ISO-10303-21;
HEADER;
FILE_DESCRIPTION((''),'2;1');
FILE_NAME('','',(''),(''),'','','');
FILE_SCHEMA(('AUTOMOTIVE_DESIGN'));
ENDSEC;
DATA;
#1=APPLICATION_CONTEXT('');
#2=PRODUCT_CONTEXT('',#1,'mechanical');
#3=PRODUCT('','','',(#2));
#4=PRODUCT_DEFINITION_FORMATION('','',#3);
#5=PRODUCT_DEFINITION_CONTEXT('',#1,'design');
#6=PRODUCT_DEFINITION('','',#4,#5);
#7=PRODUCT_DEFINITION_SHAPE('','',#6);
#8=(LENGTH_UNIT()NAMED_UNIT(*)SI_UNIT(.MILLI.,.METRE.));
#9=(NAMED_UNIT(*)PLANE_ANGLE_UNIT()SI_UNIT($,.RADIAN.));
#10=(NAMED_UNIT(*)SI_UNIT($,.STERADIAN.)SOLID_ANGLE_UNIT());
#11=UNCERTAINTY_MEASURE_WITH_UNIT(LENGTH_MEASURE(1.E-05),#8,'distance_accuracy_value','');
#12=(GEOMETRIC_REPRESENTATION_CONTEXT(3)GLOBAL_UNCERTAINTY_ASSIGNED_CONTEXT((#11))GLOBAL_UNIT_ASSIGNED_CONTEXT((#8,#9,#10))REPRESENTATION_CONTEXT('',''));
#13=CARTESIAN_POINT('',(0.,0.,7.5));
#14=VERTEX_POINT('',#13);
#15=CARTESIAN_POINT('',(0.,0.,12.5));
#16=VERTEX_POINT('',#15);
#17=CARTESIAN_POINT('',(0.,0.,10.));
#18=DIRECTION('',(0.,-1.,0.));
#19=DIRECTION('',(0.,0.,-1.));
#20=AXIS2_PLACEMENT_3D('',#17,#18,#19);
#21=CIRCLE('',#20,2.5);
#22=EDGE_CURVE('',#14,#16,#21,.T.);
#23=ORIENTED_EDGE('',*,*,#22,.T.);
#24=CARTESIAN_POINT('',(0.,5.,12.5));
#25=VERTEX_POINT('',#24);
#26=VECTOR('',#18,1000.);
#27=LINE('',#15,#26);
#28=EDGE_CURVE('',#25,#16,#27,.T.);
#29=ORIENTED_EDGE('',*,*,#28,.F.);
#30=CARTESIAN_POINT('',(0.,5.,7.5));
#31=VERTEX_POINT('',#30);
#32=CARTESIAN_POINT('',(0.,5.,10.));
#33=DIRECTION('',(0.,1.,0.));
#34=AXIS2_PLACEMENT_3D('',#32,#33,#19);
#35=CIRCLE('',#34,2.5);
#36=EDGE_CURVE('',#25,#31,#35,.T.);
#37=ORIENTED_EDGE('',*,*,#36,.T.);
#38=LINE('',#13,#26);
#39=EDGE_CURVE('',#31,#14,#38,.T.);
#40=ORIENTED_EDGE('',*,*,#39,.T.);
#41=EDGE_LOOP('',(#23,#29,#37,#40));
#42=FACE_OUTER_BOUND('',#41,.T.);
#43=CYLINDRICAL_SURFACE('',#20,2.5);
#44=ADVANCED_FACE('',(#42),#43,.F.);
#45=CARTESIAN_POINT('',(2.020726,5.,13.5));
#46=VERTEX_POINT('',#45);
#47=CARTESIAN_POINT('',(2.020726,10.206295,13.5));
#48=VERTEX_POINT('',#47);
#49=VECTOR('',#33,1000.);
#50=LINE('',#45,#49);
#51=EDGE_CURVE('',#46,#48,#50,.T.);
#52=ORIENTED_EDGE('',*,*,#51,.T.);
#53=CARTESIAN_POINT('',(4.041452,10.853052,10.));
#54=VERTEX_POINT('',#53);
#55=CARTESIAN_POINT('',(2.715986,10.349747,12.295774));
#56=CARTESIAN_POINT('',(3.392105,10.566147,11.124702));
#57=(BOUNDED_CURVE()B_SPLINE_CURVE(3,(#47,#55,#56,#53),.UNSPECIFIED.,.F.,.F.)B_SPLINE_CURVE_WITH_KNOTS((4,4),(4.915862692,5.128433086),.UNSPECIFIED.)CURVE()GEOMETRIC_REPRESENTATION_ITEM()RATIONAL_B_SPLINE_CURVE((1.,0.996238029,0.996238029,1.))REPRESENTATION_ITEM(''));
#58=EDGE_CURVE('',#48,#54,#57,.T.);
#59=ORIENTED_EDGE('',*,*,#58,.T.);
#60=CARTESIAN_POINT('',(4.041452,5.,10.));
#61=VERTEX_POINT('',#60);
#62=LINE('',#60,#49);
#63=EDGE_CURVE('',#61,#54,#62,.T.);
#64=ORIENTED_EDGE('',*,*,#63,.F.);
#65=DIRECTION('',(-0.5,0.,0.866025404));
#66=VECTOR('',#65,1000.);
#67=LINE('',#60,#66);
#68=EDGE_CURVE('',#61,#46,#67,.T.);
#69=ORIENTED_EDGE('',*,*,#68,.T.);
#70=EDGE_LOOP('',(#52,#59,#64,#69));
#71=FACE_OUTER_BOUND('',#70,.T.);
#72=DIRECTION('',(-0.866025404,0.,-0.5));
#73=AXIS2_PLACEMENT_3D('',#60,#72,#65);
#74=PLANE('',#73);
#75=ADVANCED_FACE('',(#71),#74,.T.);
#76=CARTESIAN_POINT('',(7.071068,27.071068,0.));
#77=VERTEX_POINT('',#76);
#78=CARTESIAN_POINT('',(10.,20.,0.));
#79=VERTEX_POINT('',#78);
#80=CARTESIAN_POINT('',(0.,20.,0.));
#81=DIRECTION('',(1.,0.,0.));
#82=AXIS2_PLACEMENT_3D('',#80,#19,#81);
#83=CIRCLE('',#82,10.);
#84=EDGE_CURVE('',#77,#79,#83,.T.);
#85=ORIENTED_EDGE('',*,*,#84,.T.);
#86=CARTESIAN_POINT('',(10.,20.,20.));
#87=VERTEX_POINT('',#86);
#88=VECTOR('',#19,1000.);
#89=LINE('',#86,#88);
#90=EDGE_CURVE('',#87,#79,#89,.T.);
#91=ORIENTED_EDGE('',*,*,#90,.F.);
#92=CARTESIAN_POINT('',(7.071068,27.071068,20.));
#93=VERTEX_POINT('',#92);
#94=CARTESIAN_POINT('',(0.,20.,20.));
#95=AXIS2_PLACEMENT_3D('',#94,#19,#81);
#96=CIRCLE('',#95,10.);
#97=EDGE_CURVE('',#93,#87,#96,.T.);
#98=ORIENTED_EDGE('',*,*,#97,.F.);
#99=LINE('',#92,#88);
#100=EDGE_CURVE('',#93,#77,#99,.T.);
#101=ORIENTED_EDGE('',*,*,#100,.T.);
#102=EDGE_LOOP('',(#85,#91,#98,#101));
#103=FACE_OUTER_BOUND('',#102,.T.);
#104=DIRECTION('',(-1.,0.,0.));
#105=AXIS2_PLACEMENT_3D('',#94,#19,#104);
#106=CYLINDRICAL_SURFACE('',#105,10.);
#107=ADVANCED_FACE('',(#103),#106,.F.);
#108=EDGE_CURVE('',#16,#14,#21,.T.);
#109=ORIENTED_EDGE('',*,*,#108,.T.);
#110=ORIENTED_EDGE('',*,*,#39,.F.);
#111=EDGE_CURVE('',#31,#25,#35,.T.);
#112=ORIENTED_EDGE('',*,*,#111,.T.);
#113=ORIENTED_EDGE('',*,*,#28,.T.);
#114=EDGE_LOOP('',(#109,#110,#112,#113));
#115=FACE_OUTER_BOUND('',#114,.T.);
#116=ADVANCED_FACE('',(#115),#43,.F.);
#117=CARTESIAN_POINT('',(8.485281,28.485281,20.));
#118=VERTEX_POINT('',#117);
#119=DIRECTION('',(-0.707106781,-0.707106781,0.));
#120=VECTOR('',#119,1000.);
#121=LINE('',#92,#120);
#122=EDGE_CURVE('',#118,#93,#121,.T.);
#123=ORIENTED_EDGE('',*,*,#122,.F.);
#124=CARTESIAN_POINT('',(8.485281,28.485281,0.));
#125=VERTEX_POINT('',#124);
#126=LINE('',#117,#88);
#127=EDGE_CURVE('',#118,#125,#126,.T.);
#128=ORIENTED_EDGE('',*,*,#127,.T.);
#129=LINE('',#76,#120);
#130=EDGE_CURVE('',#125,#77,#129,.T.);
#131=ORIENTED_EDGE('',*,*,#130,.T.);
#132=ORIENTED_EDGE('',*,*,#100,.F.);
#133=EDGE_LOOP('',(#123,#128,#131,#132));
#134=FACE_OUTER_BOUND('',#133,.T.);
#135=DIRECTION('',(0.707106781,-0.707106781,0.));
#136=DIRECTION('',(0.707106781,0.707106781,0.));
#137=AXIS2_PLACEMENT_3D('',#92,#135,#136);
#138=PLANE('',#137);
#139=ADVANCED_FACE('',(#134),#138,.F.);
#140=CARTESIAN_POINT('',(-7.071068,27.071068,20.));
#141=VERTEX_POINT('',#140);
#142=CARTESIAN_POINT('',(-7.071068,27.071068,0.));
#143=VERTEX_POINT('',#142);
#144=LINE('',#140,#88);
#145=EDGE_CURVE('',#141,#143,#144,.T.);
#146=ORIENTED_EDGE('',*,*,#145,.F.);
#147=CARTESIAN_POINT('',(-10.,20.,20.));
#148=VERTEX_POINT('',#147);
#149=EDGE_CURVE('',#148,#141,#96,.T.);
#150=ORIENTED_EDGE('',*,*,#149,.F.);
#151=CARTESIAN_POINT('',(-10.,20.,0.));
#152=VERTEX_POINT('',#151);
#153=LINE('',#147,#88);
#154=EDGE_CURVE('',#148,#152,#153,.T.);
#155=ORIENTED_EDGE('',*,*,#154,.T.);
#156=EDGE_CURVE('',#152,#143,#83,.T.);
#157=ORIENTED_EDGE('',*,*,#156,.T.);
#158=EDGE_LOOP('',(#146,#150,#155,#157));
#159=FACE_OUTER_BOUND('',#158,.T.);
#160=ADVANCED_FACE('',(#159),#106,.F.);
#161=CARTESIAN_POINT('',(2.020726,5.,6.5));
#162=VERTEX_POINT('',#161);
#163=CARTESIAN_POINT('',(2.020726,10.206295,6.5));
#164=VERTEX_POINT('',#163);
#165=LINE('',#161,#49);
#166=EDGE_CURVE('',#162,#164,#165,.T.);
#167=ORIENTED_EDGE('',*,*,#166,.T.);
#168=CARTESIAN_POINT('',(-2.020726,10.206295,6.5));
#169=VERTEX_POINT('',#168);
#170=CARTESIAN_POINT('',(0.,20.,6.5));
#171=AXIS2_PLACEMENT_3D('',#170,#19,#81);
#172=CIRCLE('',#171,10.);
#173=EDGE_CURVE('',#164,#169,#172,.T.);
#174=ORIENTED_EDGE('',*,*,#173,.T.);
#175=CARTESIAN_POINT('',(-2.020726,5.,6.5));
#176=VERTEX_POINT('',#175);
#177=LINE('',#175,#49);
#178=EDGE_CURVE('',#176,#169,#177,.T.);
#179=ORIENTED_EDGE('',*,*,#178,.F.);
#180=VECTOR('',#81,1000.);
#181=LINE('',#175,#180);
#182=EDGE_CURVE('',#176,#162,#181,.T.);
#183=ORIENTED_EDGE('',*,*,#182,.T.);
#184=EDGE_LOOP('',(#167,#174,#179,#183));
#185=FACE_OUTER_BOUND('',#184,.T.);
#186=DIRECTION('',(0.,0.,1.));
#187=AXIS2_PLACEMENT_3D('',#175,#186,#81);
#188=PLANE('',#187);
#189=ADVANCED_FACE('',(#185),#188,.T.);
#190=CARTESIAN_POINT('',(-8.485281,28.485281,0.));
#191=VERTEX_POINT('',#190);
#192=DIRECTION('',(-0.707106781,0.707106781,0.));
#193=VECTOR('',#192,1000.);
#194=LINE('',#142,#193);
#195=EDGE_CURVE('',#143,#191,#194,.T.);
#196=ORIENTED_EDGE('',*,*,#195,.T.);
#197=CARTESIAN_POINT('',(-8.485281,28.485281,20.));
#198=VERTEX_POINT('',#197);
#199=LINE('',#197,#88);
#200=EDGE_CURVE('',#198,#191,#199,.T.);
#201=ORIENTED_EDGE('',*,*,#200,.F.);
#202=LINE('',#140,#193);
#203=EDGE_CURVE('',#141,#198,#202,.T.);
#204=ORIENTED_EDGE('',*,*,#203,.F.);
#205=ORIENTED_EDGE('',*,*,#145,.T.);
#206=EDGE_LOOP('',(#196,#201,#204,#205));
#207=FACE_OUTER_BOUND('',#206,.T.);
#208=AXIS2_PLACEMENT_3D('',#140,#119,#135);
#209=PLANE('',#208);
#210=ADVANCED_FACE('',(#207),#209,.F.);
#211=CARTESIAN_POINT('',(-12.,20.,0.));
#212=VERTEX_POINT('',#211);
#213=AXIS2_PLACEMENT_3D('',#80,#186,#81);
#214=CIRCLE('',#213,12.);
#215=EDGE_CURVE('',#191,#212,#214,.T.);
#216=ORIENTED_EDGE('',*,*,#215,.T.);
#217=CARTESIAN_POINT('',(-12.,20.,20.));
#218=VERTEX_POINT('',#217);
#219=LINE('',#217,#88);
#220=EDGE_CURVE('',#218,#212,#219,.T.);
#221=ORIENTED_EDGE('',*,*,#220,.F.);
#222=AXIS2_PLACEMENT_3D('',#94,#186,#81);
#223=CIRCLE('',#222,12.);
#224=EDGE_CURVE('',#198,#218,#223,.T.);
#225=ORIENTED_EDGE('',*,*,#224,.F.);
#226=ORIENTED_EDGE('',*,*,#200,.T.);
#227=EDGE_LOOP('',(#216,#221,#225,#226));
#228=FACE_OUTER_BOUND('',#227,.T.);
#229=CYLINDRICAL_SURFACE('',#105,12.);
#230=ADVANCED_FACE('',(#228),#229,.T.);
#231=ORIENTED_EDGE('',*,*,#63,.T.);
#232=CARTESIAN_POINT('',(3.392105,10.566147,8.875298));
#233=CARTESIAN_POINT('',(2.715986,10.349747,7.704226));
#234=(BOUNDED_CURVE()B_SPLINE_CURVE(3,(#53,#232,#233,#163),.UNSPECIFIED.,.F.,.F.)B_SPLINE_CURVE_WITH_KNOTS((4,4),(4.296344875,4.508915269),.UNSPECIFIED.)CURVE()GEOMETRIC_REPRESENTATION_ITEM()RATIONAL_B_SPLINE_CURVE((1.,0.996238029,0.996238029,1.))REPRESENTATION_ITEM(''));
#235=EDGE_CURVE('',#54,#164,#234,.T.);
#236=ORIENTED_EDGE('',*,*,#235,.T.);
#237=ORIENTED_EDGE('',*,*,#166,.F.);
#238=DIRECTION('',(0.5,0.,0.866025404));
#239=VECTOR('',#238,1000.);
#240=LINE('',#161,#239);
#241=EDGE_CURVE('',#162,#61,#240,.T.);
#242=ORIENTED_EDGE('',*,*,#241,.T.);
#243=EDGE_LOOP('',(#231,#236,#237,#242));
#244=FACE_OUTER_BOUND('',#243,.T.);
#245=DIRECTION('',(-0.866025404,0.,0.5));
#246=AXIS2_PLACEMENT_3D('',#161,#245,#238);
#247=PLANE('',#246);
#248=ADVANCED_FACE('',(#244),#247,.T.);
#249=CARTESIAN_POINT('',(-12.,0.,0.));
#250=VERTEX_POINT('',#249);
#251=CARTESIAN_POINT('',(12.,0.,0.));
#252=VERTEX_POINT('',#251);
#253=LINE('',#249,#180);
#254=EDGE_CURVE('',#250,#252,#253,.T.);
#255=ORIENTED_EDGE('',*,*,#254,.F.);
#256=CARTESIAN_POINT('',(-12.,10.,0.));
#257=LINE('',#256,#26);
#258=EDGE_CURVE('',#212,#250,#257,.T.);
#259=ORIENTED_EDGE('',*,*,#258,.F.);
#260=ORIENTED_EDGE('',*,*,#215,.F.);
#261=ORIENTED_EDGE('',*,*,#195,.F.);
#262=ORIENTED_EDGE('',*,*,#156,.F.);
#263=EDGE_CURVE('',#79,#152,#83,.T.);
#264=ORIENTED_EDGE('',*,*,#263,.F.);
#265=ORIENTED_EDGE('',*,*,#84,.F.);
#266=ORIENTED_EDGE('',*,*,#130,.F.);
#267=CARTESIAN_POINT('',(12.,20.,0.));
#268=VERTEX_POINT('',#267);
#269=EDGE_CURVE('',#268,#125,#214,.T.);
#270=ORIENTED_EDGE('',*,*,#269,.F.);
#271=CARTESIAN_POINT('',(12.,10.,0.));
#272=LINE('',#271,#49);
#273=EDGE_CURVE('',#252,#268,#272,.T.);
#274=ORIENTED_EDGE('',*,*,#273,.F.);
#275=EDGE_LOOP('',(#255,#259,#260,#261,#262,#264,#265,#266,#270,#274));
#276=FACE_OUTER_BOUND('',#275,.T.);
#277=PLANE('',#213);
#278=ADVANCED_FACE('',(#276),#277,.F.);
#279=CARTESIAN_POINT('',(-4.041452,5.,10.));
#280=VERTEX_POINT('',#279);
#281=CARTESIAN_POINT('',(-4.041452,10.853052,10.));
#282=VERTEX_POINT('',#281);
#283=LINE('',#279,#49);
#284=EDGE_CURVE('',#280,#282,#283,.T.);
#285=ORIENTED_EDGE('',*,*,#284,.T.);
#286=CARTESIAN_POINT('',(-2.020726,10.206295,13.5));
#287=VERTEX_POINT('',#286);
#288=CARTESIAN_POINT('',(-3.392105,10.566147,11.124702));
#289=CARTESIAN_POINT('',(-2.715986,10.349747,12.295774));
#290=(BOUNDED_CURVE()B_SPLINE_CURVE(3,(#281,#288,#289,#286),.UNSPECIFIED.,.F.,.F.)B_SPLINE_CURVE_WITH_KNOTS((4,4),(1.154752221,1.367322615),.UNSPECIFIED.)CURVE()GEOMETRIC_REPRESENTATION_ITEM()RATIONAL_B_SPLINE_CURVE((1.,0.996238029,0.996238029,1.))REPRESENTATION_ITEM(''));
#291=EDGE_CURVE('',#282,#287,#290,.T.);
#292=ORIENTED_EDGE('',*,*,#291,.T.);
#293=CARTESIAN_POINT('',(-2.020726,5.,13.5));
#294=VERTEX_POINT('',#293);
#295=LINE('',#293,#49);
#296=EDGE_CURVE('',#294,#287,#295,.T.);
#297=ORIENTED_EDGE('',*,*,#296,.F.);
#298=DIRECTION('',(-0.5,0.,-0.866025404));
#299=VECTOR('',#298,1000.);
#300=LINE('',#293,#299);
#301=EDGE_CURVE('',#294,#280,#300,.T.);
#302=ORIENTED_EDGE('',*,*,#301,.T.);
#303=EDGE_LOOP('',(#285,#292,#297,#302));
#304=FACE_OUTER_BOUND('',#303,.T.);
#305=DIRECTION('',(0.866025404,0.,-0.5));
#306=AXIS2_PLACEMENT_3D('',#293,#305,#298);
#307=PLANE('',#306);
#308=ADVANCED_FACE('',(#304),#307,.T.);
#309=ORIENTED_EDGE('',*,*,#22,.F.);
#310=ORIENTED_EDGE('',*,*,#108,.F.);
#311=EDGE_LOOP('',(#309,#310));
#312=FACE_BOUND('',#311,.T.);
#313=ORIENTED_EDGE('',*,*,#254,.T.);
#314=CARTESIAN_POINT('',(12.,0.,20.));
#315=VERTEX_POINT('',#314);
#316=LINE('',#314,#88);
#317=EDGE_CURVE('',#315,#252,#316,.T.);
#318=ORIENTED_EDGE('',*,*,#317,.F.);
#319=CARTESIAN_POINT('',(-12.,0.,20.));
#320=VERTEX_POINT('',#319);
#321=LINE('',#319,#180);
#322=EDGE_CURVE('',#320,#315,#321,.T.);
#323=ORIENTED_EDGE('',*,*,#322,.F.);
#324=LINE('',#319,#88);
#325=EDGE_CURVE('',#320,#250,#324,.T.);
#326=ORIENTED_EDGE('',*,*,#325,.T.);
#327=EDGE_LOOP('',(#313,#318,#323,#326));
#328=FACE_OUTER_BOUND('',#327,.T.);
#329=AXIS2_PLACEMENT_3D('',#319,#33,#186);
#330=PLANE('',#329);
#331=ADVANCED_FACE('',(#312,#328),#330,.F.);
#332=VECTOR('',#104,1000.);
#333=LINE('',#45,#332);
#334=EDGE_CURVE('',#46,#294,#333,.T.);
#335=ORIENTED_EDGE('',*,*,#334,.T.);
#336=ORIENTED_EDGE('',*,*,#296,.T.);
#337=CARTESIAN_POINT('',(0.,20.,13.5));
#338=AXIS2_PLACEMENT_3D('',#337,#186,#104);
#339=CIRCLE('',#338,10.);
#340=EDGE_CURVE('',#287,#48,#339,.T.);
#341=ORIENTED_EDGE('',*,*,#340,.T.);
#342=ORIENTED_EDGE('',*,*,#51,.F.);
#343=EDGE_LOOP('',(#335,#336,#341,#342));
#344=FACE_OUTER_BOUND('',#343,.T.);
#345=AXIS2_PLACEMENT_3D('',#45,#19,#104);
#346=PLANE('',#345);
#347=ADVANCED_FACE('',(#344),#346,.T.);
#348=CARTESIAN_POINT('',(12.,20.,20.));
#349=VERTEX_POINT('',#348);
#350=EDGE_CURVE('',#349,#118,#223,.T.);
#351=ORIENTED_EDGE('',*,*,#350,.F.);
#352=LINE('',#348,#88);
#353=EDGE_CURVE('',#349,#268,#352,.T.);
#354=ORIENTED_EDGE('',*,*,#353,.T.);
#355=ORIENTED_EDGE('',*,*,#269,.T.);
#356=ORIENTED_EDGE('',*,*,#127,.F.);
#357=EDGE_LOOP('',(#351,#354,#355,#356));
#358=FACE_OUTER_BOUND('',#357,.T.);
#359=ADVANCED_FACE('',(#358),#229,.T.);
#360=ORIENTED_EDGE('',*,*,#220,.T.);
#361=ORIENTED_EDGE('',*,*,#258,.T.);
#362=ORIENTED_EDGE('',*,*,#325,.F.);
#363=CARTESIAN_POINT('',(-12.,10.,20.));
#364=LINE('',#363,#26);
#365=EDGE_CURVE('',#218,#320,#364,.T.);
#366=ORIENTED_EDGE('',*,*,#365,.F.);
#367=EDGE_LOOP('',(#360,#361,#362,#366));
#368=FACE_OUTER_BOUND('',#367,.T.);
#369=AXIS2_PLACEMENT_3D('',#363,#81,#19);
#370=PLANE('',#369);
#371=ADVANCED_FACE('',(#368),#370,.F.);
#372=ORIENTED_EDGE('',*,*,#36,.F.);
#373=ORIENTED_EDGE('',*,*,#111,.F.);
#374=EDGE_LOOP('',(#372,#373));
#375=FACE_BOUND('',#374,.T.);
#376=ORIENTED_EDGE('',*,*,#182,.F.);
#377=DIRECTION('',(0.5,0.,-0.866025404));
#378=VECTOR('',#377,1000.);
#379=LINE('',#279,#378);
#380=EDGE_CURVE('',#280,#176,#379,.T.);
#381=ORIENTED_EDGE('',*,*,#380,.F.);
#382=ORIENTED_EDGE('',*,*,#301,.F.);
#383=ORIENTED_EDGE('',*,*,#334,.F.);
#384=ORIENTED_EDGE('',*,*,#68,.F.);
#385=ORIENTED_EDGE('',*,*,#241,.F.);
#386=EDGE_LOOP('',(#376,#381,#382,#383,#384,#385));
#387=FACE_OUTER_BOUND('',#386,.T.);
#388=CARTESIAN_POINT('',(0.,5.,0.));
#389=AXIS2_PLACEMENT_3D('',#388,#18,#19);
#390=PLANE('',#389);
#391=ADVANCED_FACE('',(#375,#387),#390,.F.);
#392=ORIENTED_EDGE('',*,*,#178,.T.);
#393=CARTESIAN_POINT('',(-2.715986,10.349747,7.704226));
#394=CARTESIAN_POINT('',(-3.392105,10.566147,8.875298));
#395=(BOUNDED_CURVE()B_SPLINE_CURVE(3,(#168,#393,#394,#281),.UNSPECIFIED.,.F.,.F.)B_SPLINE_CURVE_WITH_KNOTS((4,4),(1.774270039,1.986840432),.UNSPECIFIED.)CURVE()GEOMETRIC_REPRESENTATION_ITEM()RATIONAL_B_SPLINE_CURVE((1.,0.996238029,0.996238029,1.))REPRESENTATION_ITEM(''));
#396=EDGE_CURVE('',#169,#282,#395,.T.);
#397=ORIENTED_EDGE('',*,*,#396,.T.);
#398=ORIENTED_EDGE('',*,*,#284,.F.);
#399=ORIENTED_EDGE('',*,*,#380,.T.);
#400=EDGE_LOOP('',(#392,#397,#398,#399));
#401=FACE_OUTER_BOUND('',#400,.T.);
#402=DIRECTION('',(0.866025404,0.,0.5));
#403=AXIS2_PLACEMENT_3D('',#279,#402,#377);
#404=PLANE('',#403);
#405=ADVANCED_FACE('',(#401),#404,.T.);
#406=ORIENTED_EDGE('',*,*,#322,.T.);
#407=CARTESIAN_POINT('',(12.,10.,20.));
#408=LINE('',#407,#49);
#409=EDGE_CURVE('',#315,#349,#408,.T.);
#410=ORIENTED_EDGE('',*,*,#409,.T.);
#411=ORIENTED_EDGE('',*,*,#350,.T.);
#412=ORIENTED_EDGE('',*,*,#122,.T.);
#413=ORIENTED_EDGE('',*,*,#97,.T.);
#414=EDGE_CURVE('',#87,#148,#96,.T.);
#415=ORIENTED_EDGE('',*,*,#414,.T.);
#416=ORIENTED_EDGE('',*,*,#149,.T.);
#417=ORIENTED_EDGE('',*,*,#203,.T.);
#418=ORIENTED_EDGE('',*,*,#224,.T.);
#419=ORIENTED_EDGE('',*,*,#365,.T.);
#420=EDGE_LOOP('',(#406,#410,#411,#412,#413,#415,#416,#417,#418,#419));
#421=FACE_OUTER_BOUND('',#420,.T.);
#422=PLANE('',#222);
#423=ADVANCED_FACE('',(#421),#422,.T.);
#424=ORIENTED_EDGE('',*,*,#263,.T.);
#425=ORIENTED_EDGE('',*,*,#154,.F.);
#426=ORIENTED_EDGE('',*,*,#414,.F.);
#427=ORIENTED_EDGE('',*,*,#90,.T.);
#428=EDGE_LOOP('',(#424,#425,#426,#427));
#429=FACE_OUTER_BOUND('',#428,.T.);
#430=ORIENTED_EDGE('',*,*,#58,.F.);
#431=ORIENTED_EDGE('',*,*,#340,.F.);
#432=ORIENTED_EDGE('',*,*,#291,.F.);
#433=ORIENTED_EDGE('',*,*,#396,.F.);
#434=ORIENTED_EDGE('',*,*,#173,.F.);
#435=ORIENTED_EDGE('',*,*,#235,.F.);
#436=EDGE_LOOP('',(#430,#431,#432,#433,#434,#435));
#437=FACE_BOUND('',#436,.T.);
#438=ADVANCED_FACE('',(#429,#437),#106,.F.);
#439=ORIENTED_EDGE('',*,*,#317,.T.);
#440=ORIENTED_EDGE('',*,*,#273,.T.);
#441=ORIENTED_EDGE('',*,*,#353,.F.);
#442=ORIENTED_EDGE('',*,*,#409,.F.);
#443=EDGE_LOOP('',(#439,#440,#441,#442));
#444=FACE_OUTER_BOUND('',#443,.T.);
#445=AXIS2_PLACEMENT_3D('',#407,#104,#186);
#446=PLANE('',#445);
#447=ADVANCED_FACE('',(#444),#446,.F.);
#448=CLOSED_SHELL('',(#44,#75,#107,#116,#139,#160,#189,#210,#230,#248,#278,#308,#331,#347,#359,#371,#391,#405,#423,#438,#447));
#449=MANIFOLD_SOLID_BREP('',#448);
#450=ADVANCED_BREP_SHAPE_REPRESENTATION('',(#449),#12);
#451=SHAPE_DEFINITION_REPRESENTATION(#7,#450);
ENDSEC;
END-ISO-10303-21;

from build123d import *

# Parameters (mm, degrees)
EXTRUDE_1_DEPTH          = 20
HOLE_WIZARD_5_0_5_1_D    = 5
CUT_EXTRUDE_3_DEPTH      = 5
CUT_EXTRUDE_3_DEPTH_BACK = 5


with BuildPart() as part:
    # 草图1 → 凸台-拉伸1 (new body)
    with BuildSketch(Plane.XY):
        with BuildLine():
            Line((-12, 10), (-12, 20))
            ThreePointArc((-12, 20), (-11.08655439, 24.592201188), (-8.485281374, 28.485281374))
            Line((-8.485281374, 28.485281374), (-7.071067812, 27.071067812))
            ThreePointArc((-7.071067812, 27.071067812), (0, 10), (7.071067812, 27.071067812))
            Line((7.071067812, 27.071067812), (8.485281374, 28.485281374))
            ThreePointArc((8.485281374, 28.485281374), (11.08655439, 24.592201188), (12, 20))
            Line((12, 20), (12, 10))
            Line((12, 10), (12, 0))
            Line((12, 0), (-12, 0))
            Line((-12, 0), (-12, 10))
        make_face()
    extrude(amount=EXTRUDE_1_DEPTH)

    # Ø5.0 (5) 直径孔1 (through all)
    with Locations(Plane(origin=(0, 0, 0), x_dir=(-1, 0, 0), z_dir=(0, -1, 0))):
        with Locations((0, -10)):
            Hole(HOLE_WIZARD_5_0_5_1_D / 2)

    # 草图7 → 切除-拉伸3 (cut, two sides: drawn at the far end of the back side and taken through both)
    with BuildSketch(Plane(origin=(0, 10, 0), x_dir=(-1, 0, 0), z_dir=(0, -1, 0)).offset(-CUT_EXTRUDE_3_DEPTH_BACK)):
        Polygon((4.041451884, -10), (2.020725942, -6.5), (-2.020725942, -6.5), (-4.041451884, -10), (-2.020725942, -13.5), (2.020725942, -13.5), align=None)
    extrude(amount=CUT_EXTRUDE_3_DEPTH + CUT_EXTRUDE_3_DEPTH_BACK, mode=Mode.SUBTRACT)


solid = part.part
